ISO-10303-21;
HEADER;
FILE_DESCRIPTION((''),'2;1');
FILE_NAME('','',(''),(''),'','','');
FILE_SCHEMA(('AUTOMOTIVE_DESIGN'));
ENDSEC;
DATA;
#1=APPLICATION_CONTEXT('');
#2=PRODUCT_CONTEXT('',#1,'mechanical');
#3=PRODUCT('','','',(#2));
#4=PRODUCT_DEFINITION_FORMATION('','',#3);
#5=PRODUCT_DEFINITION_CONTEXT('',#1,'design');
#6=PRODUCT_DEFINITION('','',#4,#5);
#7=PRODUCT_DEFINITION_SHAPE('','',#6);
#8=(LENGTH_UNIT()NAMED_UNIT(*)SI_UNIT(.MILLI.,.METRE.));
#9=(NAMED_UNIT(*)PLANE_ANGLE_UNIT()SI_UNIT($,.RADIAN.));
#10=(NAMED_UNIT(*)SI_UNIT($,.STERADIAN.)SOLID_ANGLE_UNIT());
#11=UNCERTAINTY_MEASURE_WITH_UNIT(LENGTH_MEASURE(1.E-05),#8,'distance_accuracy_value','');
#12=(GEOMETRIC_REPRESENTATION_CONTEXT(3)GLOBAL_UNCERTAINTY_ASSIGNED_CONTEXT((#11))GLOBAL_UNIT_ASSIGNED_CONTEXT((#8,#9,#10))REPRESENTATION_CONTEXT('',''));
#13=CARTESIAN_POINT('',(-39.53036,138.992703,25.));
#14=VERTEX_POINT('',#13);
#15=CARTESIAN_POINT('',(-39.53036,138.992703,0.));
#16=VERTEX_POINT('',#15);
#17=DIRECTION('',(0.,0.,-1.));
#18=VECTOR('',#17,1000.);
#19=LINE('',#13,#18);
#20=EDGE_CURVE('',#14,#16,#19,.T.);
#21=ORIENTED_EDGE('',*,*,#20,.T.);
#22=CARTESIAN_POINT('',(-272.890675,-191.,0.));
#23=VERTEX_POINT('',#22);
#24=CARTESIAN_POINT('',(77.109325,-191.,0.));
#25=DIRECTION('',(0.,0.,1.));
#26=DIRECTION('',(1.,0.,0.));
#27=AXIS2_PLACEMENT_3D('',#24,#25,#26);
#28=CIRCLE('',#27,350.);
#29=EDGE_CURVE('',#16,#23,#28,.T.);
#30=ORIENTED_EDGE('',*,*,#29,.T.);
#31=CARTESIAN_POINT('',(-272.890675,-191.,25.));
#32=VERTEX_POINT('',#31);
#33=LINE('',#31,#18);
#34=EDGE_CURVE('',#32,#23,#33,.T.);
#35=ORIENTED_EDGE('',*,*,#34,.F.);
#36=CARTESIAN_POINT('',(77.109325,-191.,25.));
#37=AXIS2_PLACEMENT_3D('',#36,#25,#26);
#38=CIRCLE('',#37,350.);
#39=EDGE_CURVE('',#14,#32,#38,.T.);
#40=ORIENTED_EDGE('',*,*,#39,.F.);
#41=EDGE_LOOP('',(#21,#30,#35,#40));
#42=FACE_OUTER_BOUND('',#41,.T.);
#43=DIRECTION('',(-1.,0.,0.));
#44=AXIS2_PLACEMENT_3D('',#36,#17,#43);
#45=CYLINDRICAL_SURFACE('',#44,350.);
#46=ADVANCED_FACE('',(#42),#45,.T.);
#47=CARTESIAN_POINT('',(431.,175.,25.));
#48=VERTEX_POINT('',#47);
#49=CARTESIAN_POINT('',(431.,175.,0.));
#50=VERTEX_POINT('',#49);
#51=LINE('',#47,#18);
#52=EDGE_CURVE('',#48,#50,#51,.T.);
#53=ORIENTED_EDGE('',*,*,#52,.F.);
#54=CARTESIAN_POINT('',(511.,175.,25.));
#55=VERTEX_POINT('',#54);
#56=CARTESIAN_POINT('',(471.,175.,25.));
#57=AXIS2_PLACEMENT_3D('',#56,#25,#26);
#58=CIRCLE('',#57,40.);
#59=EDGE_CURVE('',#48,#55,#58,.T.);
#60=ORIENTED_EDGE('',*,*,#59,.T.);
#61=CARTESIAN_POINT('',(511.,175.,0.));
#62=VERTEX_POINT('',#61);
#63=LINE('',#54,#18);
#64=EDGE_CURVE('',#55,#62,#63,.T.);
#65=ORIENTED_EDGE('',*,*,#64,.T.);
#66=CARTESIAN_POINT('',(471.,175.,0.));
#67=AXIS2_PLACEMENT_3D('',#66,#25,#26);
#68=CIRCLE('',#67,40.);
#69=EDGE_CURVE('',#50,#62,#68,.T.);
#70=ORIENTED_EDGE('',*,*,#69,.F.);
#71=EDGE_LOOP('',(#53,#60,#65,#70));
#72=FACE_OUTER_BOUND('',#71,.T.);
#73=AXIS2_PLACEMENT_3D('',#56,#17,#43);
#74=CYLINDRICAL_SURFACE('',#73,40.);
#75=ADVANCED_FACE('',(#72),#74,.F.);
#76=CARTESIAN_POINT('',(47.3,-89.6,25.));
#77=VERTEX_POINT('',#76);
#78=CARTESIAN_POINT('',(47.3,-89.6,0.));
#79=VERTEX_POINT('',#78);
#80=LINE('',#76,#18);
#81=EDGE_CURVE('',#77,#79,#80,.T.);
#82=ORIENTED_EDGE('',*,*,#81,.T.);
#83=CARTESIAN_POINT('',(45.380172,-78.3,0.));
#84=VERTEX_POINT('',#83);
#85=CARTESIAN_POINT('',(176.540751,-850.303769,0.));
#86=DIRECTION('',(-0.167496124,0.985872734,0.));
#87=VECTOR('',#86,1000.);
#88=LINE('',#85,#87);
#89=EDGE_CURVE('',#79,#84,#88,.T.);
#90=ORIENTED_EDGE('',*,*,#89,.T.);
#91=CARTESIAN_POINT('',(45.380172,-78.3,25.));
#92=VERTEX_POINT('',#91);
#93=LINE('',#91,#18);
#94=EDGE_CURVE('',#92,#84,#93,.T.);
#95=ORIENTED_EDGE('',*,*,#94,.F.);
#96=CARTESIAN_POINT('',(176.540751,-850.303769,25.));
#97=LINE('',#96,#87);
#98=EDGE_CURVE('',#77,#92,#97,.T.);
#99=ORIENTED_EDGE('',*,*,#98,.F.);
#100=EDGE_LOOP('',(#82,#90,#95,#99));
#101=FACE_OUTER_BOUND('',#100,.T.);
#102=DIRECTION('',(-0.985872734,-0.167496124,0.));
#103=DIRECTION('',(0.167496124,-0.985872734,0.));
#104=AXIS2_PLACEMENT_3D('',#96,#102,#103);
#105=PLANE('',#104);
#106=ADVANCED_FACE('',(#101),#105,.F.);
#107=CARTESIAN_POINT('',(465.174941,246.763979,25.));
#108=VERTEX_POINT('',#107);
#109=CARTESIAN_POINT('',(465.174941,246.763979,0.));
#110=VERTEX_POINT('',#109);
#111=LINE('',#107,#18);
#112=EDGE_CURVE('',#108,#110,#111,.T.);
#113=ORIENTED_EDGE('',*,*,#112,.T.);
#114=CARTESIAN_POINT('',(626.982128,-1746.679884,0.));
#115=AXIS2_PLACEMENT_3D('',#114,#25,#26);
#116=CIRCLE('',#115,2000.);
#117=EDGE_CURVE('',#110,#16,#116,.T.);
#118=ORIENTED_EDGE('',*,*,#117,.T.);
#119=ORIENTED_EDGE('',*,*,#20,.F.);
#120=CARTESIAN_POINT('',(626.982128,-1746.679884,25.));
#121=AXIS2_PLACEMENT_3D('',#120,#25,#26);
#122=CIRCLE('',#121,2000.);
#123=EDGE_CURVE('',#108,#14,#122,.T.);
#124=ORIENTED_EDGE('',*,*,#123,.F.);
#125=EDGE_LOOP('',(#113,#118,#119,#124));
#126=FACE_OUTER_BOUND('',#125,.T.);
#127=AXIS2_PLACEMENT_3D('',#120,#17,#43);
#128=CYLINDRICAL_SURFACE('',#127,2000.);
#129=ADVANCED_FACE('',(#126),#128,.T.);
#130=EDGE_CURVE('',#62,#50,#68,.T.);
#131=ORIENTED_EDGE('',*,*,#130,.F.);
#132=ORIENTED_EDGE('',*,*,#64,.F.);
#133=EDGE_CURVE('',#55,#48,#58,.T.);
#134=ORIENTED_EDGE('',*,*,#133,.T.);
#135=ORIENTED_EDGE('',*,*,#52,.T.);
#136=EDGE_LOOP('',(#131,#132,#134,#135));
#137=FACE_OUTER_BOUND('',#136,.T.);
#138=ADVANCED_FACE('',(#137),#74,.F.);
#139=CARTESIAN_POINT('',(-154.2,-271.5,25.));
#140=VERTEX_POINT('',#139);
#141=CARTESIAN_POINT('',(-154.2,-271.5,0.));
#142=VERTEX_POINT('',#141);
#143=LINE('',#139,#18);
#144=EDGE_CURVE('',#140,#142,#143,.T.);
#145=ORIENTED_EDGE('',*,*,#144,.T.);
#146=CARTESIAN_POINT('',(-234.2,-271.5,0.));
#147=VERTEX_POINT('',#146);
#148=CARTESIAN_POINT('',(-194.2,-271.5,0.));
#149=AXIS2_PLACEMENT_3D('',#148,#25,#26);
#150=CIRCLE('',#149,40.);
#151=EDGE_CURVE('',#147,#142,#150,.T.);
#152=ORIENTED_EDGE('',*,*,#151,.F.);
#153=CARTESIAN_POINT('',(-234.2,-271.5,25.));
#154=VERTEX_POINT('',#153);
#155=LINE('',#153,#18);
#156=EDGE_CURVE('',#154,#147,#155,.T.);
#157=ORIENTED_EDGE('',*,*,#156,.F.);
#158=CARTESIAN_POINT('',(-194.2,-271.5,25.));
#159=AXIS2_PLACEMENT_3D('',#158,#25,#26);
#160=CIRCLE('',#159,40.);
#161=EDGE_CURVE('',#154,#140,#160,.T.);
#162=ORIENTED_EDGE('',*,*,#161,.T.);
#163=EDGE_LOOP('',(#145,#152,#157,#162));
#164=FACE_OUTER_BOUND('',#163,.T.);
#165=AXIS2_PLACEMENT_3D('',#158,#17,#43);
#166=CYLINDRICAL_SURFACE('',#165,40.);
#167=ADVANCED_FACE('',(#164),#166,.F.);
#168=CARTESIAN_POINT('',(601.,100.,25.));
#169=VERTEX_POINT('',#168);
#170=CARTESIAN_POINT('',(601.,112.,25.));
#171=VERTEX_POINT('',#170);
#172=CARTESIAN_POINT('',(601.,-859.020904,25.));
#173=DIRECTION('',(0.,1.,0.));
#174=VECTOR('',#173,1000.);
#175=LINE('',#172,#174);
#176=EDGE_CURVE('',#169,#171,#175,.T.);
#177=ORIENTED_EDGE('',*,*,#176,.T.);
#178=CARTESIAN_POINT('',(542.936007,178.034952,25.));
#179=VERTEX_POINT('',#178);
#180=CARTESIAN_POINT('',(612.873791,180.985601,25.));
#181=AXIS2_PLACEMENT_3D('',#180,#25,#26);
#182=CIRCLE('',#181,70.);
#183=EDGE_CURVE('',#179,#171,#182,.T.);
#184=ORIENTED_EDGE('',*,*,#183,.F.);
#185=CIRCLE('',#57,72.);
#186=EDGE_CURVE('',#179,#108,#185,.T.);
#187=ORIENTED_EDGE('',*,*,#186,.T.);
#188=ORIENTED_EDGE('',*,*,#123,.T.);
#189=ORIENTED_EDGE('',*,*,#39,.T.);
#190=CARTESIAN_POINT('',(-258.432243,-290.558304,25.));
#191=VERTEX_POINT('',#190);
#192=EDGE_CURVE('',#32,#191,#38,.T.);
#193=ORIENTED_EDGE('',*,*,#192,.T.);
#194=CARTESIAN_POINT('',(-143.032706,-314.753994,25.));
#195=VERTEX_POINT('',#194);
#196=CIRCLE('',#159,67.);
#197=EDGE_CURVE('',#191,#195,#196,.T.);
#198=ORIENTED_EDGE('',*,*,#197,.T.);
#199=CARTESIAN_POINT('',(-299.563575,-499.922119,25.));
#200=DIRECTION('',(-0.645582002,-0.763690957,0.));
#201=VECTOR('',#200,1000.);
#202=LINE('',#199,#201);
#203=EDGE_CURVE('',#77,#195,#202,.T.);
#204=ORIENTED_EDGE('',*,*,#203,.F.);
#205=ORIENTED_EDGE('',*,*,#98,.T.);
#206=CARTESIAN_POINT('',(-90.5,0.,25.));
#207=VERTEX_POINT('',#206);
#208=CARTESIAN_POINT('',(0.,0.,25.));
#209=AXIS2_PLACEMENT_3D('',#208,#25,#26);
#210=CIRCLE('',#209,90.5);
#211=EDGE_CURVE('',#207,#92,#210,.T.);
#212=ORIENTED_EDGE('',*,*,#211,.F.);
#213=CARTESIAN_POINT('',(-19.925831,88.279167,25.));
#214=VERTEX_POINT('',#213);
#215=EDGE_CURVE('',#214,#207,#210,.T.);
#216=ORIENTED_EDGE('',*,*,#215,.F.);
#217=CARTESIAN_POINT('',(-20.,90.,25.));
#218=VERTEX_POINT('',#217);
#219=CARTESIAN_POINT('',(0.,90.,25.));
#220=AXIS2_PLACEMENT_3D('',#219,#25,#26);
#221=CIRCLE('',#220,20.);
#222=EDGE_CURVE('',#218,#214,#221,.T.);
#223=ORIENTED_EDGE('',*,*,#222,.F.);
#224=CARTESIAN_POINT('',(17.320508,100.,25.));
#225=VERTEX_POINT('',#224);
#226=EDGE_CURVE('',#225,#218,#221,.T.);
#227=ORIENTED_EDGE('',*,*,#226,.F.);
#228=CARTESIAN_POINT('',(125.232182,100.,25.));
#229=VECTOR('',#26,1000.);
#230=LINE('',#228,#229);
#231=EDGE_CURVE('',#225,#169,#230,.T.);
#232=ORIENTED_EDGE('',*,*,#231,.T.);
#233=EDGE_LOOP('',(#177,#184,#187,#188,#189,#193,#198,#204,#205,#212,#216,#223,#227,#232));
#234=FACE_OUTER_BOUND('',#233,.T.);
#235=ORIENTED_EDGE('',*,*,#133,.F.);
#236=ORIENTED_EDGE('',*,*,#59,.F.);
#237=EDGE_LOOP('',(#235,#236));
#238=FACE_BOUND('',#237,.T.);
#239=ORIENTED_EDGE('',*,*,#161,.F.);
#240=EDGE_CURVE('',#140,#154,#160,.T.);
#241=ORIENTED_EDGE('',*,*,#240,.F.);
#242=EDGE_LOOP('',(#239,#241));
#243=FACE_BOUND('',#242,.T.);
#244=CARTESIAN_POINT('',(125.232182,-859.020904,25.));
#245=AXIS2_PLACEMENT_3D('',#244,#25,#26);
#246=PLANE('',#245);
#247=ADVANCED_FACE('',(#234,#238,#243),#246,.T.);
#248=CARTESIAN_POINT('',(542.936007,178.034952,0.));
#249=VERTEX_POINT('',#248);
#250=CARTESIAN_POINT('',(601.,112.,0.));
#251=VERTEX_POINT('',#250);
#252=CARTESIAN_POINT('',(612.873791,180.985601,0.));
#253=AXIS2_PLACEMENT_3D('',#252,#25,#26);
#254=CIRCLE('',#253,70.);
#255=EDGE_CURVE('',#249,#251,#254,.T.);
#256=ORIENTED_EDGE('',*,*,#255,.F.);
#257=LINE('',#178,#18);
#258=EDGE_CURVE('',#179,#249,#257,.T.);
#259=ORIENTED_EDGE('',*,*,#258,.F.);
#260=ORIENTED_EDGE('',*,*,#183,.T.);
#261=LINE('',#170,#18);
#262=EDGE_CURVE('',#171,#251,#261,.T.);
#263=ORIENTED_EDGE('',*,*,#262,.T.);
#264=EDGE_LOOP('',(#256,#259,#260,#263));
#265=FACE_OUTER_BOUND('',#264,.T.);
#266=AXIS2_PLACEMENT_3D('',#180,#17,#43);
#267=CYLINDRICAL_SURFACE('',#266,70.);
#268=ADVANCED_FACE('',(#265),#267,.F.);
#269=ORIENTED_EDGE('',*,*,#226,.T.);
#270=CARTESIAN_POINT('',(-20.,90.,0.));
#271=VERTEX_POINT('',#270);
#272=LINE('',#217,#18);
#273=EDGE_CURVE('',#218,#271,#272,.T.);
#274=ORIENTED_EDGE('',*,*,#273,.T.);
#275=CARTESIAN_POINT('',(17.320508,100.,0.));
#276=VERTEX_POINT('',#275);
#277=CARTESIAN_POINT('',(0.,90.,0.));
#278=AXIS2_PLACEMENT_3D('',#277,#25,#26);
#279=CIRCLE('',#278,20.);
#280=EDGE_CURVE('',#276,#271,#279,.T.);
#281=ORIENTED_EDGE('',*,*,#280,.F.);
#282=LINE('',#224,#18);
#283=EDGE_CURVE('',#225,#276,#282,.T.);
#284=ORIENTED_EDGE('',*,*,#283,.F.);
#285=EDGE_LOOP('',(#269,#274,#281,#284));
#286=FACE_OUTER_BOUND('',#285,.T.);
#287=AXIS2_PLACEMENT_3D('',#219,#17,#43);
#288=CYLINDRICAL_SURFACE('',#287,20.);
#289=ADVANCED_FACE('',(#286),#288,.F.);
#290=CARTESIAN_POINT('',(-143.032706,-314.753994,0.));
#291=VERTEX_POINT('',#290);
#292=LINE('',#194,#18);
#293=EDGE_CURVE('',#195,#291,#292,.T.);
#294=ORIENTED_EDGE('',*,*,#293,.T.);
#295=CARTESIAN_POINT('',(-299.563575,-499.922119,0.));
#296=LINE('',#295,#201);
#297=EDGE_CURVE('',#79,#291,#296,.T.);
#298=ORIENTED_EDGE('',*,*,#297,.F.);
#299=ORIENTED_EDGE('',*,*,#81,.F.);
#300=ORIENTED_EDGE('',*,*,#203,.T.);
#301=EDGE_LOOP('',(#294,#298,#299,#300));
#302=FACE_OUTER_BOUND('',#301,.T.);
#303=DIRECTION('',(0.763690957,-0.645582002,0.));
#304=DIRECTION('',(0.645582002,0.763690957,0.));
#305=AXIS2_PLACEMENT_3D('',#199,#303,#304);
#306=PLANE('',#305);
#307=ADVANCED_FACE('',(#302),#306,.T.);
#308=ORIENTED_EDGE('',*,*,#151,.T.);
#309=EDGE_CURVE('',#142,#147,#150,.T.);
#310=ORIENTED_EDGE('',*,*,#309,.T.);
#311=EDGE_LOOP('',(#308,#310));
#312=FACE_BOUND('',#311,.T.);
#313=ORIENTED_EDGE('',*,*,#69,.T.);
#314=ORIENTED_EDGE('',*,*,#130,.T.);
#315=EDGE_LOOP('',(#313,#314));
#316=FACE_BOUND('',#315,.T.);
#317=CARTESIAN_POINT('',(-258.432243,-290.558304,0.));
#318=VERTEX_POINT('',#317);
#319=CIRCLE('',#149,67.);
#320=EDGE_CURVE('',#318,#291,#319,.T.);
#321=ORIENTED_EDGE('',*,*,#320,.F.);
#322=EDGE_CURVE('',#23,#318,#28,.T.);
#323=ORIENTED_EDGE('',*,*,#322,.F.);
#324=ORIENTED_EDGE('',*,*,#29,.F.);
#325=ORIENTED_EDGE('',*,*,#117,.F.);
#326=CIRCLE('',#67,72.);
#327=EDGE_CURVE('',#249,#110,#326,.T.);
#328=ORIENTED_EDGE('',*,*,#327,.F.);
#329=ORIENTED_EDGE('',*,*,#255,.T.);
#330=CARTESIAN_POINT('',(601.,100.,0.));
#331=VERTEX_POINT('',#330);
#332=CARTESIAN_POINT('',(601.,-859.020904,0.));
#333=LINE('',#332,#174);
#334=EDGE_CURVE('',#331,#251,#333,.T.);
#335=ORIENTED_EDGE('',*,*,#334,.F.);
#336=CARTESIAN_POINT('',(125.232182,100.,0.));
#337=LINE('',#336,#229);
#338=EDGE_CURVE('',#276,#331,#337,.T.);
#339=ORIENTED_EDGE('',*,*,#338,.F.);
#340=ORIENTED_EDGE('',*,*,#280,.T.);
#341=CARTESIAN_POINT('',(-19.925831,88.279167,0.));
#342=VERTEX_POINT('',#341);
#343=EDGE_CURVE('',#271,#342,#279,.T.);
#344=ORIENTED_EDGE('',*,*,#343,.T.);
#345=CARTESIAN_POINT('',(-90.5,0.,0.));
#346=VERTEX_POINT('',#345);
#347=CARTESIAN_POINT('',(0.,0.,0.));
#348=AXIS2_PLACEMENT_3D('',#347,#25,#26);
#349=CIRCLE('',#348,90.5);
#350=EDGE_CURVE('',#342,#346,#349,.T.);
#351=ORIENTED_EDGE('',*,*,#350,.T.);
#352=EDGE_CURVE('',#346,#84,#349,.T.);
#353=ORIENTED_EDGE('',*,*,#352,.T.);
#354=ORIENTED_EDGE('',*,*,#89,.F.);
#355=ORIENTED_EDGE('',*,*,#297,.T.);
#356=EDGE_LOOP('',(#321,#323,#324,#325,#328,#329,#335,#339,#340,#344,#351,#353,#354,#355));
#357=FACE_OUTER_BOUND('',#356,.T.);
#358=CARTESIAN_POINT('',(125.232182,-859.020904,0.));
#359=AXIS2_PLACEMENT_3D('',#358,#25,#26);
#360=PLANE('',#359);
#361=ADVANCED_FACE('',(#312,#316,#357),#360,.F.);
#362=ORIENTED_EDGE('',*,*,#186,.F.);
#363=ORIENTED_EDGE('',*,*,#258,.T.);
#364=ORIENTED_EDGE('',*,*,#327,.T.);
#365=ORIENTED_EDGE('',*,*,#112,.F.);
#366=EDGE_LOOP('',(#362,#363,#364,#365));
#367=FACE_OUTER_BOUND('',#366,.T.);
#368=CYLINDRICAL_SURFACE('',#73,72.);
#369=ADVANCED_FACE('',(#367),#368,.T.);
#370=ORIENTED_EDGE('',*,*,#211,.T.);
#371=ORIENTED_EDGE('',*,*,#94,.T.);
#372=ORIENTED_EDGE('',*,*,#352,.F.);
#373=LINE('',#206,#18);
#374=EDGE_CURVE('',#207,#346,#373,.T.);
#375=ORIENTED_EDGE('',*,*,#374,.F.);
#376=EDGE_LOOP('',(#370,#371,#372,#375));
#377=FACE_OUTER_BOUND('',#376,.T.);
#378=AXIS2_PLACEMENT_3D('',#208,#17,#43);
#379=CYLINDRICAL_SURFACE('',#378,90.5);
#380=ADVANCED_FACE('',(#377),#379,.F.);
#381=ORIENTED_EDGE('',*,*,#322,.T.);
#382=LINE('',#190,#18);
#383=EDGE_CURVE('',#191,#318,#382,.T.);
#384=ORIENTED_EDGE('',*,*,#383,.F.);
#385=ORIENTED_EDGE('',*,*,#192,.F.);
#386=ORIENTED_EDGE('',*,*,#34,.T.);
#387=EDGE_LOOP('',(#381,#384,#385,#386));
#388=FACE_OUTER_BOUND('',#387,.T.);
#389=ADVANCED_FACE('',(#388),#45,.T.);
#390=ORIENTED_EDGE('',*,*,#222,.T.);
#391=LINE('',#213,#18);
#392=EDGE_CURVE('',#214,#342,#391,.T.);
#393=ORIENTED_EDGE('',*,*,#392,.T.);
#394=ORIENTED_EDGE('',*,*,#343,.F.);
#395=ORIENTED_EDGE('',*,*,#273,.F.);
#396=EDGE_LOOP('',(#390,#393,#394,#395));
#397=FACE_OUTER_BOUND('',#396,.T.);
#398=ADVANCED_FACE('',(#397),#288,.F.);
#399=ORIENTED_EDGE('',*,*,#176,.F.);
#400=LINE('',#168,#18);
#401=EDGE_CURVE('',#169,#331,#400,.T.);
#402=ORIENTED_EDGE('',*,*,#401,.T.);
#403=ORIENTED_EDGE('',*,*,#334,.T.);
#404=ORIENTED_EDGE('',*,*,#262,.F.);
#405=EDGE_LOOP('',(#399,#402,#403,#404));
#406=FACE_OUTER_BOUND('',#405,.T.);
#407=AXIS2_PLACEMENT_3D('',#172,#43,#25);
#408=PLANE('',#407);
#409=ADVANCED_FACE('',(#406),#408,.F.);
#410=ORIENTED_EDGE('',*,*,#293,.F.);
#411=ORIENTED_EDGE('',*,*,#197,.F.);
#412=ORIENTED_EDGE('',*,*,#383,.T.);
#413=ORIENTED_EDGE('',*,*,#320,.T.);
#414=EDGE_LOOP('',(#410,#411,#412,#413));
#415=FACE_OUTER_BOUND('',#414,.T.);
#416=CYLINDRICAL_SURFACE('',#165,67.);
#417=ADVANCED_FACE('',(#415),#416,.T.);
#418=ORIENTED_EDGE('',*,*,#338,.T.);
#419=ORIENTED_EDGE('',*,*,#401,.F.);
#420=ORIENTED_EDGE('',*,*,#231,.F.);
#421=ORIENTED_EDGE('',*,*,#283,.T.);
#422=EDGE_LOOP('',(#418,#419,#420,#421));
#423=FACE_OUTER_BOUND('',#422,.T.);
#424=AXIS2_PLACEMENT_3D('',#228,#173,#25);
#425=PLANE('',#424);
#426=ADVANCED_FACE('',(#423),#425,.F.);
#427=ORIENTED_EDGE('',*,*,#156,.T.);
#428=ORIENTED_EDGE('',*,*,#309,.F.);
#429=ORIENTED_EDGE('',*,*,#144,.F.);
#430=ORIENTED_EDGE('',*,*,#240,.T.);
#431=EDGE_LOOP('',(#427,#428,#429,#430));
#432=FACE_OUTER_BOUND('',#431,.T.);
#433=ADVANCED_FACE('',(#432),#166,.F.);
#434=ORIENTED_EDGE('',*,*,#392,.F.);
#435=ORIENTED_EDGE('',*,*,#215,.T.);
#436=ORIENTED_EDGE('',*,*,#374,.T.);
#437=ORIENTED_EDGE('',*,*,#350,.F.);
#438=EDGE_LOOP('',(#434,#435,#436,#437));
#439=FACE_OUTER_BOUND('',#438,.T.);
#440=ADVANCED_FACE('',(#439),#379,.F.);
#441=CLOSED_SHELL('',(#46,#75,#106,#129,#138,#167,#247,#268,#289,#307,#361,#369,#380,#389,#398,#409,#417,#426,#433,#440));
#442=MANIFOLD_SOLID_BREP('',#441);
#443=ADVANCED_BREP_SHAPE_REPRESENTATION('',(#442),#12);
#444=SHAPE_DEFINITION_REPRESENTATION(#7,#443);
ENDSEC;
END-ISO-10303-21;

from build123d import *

# Parameters (mm, degrees)
SKETCH1_R           = 40
BOSS_EXTRUDE1_DEPTH = 25


with BuildPart() as part:
    # Sketch1 → Boss-Extrude1 (new body)
    with BuildSketch(Plane.XY):
        with BuildLine():
            Line((17.320508076, 100), (601, 100))
            Line((601, 100), (601, 112))
            ThreePointArc((601, 112), (560.305386081, 134.762632261), (542.936006728, 178.034952402))
            ThreePointArc((542.936006728, 178.034952402), (518.682115493, 228.948270242), (465.174941276, 246.763979062))
            ThreePointArc((465.174941276, 246.763979062), (209.331516914, 209.226035995), (-39.530360121, 138.99270262))
            ThreePointArc((-39.530360121, 138.99270262), (-234.732763539, -32.083318616), (-258.432243095, -290.558303887))
            ThreePointArc((-258.432243095, -290.558303887), (-207.948857392, -337.074148263), (-143.032705856, -314.75399415))
            Line((-143.032705856, -314.75399415), (47.3, -89.6))
            Line((47.3, -89.6), (45.380171882, -78.3))
            ThreePointArc((45.380171882, -78.3), (-84.25636808, -33.032021404), (-19.925830789, 88.279166667))
            ThreePointArc((-19.925830789, 88.279166667), (-6.003449851, 109.077698758), (17.320508076, 100))
        make_face()
        with Locations((-194.2, -271.5)):
            Circle(SKETCH1_R, mode=Mode.SUBTRACT)
        with Locations((471, 175)):
            Circle(SKETCH1_R, mode=Mode.SUBTRACT)
    extrude(amount=BOSS_EXTRUDE1_DEPTH)


solid = part.part
